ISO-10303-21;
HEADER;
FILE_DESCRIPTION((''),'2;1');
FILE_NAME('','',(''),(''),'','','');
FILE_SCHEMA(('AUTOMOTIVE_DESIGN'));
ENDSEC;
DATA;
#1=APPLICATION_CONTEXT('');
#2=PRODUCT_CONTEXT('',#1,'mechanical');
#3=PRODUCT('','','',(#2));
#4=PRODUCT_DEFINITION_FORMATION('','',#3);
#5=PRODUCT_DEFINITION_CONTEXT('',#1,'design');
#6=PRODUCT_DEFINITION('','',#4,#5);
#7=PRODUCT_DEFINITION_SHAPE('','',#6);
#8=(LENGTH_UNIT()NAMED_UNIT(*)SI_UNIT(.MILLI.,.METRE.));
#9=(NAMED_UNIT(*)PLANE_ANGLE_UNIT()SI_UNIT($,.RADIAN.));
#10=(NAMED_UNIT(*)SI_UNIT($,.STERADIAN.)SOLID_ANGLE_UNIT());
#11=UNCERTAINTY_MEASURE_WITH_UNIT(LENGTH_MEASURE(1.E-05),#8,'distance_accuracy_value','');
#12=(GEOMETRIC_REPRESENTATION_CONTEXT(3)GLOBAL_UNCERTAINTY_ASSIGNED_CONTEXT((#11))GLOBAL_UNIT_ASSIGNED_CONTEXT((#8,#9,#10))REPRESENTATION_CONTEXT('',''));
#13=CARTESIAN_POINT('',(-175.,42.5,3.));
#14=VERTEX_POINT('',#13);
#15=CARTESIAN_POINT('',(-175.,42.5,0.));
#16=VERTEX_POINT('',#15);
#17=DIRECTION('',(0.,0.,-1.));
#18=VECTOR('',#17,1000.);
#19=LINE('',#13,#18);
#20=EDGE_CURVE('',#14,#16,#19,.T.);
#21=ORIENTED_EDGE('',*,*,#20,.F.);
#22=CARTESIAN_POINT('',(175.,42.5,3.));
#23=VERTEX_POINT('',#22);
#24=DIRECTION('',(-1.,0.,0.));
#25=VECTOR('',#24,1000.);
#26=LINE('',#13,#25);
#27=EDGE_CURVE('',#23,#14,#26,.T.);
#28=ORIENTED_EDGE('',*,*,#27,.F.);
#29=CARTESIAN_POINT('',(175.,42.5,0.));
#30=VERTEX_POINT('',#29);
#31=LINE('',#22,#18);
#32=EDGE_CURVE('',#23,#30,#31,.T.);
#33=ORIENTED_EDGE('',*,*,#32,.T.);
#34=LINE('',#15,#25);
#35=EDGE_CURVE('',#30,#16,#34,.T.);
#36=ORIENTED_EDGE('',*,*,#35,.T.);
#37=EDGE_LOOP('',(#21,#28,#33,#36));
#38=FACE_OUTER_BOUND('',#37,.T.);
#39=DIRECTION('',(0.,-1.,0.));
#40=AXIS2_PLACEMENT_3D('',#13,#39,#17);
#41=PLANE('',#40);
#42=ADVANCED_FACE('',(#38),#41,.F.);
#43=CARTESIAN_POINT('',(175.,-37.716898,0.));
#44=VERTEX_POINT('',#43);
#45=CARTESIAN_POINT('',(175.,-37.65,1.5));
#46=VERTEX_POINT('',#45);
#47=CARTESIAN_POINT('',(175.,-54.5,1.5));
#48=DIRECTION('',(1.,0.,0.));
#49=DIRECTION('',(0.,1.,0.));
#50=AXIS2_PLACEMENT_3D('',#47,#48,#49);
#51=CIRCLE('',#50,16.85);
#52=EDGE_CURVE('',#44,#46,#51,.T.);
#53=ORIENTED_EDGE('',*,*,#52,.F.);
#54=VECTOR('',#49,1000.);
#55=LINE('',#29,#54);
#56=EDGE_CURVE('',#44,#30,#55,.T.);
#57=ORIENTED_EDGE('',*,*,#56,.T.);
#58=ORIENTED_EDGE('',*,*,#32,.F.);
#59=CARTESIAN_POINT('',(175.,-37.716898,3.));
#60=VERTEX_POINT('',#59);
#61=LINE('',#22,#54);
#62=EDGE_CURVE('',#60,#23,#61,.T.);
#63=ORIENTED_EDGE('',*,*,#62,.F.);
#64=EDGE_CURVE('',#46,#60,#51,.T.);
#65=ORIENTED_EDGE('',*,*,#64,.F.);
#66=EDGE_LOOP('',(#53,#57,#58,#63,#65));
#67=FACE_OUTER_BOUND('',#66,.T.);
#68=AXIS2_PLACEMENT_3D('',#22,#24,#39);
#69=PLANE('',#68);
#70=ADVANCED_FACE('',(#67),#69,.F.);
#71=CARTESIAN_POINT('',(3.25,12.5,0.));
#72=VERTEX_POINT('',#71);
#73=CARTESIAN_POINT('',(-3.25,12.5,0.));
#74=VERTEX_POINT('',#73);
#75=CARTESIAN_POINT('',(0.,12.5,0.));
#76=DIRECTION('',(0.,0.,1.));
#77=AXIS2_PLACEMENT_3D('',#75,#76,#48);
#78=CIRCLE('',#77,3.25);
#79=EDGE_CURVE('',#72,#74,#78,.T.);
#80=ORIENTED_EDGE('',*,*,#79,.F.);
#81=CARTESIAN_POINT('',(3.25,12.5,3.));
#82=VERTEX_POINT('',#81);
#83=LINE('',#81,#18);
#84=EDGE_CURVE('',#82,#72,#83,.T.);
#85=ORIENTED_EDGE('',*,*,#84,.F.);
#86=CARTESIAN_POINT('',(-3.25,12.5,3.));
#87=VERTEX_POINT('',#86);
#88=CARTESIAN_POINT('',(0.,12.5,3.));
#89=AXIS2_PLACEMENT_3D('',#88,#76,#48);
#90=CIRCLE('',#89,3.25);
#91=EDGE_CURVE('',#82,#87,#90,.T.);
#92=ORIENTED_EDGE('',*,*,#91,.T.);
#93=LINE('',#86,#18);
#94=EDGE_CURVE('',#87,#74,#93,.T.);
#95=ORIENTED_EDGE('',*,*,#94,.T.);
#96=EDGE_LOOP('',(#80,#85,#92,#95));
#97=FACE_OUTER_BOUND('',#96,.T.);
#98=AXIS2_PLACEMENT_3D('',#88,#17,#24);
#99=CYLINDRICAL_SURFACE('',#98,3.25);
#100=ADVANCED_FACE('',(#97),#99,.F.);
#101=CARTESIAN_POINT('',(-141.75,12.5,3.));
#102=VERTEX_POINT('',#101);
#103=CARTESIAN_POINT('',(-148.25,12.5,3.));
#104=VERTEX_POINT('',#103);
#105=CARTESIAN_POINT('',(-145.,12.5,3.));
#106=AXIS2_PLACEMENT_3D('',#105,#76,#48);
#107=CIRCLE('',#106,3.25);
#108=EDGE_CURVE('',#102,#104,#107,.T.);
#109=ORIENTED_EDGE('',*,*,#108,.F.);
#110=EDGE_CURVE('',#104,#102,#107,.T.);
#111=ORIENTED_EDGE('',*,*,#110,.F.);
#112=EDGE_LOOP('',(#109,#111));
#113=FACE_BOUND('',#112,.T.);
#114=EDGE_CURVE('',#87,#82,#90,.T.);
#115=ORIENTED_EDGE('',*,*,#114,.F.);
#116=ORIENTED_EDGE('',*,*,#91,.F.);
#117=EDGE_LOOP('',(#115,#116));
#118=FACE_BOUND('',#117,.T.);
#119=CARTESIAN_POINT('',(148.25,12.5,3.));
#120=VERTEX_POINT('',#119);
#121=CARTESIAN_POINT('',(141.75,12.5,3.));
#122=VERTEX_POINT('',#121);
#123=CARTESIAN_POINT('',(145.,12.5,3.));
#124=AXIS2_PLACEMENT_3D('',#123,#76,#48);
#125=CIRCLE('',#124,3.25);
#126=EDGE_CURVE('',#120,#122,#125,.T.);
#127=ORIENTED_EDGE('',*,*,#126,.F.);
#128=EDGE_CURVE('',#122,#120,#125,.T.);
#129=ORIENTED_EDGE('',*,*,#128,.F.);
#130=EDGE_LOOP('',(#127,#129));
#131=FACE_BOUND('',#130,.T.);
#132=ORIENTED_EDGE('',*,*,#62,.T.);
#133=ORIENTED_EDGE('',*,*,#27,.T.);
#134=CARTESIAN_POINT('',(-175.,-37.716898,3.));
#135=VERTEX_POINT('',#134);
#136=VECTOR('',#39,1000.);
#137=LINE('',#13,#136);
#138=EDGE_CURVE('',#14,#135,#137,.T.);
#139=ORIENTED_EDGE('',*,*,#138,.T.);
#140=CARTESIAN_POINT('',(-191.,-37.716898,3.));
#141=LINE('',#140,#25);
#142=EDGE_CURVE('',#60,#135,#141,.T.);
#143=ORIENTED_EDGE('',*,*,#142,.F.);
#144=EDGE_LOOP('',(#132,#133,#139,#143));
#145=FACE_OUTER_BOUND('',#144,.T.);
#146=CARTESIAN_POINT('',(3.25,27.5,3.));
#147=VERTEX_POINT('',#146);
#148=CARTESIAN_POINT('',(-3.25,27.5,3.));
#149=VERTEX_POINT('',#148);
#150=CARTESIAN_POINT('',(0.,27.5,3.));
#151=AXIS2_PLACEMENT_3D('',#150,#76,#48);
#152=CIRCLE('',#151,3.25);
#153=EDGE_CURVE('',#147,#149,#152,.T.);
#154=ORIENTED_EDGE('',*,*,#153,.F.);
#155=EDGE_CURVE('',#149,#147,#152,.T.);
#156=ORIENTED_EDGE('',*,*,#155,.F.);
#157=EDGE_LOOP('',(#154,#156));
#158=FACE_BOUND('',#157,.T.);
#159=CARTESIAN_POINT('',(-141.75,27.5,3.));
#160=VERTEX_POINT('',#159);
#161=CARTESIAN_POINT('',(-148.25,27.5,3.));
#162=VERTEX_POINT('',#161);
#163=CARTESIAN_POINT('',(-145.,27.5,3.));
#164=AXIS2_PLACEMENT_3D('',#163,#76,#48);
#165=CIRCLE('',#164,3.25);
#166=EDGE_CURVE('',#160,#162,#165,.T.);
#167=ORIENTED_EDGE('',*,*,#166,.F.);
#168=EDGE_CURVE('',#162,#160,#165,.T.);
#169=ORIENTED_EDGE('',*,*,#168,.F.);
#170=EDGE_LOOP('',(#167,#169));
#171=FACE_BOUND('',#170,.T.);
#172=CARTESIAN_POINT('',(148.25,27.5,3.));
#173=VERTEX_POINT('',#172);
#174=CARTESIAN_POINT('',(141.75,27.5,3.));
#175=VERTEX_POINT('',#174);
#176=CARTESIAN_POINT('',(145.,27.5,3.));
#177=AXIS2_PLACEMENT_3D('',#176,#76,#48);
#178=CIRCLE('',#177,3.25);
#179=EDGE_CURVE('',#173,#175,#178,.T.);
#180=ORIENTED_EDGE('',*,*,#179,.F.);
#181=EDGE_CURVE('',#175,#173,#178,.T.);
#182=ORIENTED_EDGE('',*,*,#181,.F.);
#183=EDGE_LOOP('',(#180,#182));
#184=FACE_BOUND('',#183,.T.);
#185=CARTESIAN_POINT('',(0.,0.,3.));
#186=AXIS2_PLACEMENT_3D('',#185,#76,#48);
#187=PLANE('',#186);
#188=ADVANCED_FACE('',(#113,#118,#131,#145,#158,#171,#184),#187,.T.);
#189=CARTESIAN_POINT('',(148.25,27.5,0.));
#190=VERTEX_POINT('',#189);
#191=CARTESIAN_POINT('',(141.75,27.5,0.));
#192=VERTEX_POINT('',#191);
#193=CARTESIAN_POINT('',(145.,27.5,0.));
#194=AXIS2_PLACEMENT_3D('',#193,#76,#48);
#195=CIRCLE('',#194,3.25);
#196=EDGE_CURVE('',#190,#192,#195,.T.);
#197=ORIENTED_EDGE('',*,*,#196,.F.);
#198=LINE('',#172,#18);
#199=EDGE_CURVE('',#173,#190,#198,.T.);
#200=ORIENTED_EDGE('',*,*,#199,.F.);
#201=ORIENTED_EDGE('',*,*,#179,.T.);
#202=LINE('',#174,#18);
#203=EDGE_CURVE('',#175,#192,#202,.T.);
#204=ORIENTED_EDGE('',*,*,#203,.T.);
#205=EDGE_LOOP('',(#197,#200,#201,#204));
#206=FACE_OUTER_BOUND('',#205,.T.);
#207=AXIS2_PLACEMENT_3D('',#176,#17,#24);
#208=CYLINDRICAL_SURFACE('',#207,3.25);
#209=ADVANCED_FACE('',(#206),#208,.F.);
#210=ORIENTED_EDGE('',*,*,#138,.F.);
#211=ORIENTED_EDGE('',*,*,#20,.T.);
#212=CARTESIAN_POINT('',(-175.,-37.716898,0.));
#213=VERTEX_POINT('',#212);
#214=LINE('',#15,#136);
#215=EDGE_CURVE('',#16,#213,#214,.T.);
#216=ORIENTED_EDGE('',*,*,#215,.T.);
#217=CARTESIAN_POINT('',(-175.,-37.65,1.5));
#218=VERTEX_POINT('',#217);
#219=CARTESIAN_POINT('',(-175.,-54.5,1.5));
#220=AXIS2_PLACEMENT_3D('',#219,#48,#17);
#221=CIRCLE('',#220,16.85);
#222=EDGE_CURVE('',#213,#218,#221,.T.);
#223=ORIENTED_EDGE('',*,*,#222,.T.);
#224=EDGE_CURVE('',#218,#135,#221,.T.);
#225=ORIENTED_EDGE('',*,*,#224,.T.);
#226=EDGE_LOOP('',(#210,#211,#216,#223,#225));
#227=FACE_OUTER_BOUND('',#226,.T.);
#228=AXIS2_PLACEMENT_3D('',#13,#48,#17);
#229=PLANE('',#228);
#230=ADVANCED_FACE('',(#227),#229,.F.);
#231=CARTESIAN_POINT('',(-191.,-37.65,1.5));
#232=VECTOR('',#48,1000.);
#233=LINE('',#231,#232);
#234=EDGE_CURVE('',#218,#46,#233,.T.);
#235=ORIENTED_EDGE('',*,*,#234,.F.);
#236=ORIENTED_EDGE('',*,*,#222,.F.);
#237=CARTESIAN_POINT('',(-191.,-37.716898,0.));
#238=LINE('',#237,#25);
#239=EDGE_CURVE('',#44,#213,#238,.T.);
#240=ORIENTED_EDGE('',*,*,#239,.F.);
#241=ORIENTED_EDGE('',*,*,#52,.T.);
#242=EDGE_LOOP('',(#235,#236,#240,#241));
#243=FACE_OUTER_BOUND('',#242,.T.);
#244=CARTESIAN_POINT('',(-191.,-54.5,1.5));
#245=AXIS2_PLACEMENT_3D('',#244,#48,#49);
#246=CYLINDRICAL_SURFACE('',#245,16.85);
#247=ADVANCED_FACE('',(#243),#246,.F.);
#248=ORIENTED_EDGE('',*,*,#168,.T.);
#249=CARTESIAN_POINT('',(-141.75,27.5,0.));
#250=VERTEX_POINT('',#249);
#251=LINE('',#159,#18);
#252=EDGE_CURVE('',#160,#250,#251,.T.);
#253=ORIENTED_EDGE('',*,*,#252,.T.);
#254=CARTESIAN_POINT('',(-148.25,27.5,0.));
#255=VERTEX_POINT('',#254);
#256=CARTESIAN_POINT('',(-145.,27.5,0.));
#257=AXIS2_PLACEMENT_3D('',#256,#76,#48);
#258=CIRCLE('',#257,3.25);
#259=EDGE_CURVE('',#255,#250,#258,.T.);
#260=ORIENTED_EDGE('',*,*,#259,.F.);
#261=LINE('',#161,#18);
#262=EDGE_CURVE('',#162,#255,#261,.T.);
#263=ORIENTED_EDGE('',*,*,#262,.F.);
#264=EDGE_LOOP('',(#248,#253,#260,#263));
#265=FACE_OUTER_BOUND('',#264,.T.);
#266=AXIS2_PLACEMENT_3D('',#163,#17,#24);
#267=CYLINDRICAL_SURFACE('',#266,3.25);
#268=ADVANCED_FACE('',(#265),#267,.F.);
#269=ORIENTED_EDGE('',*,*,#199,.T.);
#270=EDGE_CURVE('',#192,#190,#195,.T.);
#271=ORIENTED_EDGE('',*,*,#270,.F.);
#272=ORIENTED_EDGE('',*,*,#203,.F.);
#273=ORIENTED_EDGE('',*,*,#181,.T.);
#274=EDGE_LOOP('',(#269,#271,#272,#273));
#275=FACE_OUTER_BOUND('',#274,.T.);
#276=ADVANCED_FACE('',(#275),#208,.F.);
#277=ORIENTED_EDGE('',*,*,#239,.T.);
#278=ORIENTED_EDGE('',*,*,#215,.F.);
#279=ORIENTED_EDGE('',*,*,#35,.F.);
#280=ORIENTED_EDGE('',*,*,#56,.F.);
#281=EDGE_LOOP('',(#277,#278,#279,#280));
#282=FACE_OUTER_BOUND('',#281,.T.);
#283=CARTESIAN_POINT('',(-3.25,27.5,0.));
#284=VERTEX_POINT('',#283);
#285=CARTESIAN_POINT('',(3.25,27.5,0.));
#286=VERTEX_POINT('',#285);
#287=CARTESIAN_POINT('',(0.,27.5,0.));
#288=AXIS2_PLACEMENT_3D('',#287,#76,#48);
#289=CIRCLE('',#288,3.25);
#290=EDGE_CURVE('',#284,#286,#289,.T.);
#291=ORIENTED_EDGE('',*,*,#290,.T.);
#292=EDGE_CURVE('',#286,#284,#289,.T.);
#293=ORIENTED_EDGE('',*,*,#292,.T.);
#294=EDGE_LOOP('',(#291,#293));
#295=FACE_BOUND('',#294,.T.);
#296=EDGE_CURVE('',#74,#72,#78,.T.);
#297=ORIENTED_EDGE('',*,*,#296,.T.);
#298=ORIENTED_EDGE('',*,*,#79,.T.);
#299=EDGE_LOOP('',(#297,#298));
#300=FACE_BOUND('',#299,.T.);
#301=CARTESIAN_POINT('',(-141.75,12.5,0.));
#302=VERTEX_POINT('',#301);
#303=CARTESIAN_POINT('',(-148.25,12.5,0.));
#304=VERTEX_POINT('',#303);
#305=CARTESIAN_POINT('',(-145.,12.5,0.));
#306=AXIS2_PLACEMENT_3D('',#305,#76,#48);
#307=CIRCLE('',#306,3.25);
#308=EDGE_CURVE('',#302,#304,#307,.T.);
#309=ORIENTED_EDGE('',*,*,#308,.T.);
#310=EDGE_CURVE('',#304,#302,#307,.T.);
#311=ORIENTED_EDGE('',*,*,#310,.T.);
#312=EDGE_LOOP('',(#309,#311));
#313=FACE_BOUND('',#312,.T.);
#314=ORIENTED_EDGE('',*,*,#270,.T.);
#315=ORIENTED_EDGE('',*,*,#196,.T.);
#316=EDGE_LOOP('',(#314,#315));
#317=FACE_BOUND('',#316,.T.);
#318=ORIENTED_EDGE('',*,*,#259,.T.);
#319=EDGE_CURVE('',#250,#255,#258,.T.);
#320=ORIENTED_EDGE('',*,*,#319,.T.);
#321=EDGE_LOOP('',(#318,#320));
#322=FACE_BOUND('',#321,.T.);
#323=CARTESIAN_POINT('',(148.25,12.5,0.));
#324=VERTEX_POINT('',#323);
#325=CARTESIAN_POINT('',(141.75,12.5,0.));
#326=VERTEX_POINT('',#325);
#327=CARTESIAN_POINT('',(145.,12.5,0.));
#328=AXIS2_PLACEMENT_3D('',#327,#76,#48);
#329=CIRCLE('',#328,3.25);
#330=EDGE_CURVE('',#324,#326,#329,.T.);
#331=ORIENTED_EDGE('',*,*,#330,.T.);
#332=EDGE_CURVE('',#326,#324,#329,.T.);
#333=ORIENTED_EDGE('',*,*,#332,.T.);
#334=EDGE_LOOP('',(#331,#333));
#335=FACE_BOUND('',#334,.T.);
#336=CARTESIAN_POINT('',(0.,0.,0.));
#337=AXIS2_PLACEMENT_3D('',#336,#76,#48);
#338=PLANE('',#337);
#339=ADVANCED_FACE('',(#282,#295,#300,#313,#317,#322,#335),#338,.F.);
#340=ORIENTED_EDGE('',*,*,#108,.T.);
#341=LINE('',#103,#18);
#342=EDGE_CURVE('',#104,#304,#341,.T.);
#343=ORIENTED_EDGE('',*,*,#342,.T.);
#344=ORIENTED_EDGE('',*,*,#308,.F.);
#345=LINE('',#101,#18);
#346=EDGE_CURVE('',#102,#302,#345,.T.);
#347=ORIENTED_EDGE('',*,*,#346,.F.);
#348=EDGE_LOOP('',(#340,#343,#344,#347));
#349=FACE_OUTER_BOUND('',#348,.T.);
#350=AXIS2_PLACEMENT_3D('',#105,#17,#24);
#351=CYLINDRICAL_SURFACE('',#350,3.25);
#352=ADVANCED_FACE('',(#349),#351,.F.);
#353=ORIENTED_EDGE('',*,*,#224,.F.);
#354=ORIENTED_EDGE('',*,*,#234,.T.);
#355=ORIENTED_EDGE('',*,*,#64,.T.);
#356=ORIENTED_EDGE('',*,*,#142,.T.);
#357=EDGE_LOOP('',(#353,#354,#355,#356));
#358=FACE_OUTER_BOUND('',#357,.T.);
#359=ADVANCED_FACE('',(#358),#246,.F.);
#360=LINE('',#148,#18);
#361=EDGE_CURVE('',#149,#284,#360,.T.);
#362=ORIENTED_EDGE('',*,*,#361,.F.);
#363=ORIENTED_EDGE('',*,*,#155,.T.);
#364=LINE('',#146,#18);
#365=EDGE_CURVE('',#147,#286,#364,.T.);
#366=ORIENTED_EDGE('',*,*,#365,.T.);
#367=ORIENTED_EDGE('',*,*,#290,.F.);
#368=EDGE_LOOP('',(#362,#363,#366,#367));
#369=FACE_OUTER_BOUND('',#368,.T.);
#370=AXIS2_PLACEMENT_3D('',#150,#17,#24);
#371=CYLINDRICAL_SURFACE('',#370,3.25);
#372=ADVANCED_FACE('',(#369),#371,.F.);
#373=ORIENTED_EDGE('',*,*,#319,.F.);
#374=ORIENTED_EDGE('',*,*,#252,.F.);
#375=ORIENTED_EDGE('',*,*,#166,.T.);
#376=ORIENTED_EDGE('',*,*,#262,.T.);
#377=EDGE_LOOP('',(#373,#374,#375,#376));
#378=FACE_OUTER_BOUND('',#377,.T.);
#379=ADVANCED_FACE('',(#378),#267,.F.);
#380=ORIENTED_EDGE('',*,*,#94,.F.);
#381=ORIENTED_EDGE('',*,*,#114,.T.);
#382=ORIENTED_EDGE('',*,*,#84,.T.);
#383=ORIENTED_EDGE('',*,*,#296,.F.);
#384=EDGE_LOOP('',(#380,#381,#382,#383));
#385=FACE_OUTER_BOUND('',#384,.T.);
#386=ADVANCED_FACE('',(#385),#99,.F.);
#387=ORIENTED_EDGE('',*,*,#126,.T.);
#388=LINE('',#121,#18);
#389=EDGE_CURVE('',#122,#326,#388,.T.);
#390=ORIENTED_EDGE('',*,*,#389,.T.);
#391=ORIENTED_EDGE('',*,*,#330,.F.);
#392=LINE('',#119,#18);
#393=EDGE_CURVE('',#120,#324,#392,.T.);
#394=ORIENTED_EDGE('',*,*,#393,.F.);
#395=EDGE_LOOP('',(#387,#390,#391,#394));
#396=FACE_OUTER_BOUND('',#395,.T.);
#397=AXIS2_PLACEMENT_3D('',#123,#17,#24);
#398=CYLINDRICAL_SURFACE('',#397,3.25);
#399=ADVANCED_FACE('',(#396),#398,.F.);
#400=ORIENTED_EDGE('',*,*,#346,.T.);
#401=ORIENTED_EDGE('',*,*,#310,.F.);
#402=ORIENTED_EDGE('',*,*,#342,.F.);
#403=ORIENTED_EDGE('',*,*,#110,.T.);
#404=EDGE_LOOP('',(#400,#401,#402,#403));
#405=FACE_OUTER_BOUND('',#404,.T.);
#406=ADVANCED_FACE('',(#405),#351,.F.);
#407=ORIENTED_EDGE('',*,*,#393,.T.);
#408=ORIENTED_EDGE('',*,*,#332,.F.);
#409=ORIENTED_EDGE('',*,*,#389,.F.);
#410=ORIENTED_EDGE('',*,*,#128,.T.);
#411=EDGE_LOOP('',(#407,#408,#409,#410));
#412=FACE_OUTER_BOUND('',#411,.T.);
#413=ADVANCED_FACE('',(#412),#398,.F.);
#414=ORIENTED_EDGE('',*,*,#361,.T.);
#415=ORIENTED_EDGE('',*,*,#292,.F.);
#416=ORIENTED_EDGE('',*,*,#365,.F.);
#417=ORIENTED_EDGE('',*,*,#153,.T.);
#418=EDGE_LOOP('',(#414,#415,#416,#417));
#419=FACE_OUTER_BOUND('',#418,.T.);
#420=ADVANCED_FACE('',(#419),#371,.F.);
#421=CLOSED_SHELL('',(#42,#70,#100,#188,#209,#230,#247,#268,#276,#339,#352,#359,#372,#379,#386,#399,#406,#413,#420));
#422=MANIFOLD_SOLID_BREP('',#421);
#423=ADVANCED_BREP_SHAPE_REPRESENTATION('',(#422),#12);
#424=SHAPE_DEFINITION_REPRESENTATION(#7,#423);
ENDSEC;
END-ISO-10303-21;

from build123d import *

# Parameters (mm, degrees)
SKETCH_1_W          = 350
SKETCH_1_H          = 85
SKETCH_1_R          = 3.25
EXTRUDE_1_DEPTH     = 3
SKETCH_2_R          = 16.85
CUT_EXTRUDE_1_DEPTH = 366


with BuildPart() as part:
    # 草图1 → 凸台-拉伸1 (new body)
    with BuildSketch(Plane.XY):
        Rectangle(SKETCH_1_W, SKETCH_1_H)
        with Locations((-145, 27.5)):
            Circle(SKETCH_1_R, mode=Mode.SUBTRACT)
        with Locations((-145, 12.5)):
            Circle(SKETCH_1_R, mode=Mode.SUBTRACT)
        with Locations((0, 27.5)):
            Circle(SKETCH_1_R, mode=Mode.SUBTRACT)
        with Locations((0, 12.5)):
            Circle(SKETCH_1_R, mode=Mode.SUBTRACT)
        with Locations((145, 27.5)):
            Circle(SKETCH_1_R, mode=Mode.SUBTRACT)
        with Locations((145, 12.5)):
            Circle(SKETCH_1_R, mode=Mode.SUBTRACT)
    extrude(amount=EXTRUDE_1_DEPTH)

    # 草图2 → 切除-拉伸1 (cut)
    with BuildSketch(Plane(origin=(175, 0, 0), x_dir=(0, 0, -1), z_dir=(1, 0, 0))):
        with Locations((-1.5, -54.5)):
            Circle(SKETCH_2_R)
    extrude(amount=-CUT_EXTRUDE_1_DEPTH, mode=Mode.SUBTRACT)


solid = part.part
